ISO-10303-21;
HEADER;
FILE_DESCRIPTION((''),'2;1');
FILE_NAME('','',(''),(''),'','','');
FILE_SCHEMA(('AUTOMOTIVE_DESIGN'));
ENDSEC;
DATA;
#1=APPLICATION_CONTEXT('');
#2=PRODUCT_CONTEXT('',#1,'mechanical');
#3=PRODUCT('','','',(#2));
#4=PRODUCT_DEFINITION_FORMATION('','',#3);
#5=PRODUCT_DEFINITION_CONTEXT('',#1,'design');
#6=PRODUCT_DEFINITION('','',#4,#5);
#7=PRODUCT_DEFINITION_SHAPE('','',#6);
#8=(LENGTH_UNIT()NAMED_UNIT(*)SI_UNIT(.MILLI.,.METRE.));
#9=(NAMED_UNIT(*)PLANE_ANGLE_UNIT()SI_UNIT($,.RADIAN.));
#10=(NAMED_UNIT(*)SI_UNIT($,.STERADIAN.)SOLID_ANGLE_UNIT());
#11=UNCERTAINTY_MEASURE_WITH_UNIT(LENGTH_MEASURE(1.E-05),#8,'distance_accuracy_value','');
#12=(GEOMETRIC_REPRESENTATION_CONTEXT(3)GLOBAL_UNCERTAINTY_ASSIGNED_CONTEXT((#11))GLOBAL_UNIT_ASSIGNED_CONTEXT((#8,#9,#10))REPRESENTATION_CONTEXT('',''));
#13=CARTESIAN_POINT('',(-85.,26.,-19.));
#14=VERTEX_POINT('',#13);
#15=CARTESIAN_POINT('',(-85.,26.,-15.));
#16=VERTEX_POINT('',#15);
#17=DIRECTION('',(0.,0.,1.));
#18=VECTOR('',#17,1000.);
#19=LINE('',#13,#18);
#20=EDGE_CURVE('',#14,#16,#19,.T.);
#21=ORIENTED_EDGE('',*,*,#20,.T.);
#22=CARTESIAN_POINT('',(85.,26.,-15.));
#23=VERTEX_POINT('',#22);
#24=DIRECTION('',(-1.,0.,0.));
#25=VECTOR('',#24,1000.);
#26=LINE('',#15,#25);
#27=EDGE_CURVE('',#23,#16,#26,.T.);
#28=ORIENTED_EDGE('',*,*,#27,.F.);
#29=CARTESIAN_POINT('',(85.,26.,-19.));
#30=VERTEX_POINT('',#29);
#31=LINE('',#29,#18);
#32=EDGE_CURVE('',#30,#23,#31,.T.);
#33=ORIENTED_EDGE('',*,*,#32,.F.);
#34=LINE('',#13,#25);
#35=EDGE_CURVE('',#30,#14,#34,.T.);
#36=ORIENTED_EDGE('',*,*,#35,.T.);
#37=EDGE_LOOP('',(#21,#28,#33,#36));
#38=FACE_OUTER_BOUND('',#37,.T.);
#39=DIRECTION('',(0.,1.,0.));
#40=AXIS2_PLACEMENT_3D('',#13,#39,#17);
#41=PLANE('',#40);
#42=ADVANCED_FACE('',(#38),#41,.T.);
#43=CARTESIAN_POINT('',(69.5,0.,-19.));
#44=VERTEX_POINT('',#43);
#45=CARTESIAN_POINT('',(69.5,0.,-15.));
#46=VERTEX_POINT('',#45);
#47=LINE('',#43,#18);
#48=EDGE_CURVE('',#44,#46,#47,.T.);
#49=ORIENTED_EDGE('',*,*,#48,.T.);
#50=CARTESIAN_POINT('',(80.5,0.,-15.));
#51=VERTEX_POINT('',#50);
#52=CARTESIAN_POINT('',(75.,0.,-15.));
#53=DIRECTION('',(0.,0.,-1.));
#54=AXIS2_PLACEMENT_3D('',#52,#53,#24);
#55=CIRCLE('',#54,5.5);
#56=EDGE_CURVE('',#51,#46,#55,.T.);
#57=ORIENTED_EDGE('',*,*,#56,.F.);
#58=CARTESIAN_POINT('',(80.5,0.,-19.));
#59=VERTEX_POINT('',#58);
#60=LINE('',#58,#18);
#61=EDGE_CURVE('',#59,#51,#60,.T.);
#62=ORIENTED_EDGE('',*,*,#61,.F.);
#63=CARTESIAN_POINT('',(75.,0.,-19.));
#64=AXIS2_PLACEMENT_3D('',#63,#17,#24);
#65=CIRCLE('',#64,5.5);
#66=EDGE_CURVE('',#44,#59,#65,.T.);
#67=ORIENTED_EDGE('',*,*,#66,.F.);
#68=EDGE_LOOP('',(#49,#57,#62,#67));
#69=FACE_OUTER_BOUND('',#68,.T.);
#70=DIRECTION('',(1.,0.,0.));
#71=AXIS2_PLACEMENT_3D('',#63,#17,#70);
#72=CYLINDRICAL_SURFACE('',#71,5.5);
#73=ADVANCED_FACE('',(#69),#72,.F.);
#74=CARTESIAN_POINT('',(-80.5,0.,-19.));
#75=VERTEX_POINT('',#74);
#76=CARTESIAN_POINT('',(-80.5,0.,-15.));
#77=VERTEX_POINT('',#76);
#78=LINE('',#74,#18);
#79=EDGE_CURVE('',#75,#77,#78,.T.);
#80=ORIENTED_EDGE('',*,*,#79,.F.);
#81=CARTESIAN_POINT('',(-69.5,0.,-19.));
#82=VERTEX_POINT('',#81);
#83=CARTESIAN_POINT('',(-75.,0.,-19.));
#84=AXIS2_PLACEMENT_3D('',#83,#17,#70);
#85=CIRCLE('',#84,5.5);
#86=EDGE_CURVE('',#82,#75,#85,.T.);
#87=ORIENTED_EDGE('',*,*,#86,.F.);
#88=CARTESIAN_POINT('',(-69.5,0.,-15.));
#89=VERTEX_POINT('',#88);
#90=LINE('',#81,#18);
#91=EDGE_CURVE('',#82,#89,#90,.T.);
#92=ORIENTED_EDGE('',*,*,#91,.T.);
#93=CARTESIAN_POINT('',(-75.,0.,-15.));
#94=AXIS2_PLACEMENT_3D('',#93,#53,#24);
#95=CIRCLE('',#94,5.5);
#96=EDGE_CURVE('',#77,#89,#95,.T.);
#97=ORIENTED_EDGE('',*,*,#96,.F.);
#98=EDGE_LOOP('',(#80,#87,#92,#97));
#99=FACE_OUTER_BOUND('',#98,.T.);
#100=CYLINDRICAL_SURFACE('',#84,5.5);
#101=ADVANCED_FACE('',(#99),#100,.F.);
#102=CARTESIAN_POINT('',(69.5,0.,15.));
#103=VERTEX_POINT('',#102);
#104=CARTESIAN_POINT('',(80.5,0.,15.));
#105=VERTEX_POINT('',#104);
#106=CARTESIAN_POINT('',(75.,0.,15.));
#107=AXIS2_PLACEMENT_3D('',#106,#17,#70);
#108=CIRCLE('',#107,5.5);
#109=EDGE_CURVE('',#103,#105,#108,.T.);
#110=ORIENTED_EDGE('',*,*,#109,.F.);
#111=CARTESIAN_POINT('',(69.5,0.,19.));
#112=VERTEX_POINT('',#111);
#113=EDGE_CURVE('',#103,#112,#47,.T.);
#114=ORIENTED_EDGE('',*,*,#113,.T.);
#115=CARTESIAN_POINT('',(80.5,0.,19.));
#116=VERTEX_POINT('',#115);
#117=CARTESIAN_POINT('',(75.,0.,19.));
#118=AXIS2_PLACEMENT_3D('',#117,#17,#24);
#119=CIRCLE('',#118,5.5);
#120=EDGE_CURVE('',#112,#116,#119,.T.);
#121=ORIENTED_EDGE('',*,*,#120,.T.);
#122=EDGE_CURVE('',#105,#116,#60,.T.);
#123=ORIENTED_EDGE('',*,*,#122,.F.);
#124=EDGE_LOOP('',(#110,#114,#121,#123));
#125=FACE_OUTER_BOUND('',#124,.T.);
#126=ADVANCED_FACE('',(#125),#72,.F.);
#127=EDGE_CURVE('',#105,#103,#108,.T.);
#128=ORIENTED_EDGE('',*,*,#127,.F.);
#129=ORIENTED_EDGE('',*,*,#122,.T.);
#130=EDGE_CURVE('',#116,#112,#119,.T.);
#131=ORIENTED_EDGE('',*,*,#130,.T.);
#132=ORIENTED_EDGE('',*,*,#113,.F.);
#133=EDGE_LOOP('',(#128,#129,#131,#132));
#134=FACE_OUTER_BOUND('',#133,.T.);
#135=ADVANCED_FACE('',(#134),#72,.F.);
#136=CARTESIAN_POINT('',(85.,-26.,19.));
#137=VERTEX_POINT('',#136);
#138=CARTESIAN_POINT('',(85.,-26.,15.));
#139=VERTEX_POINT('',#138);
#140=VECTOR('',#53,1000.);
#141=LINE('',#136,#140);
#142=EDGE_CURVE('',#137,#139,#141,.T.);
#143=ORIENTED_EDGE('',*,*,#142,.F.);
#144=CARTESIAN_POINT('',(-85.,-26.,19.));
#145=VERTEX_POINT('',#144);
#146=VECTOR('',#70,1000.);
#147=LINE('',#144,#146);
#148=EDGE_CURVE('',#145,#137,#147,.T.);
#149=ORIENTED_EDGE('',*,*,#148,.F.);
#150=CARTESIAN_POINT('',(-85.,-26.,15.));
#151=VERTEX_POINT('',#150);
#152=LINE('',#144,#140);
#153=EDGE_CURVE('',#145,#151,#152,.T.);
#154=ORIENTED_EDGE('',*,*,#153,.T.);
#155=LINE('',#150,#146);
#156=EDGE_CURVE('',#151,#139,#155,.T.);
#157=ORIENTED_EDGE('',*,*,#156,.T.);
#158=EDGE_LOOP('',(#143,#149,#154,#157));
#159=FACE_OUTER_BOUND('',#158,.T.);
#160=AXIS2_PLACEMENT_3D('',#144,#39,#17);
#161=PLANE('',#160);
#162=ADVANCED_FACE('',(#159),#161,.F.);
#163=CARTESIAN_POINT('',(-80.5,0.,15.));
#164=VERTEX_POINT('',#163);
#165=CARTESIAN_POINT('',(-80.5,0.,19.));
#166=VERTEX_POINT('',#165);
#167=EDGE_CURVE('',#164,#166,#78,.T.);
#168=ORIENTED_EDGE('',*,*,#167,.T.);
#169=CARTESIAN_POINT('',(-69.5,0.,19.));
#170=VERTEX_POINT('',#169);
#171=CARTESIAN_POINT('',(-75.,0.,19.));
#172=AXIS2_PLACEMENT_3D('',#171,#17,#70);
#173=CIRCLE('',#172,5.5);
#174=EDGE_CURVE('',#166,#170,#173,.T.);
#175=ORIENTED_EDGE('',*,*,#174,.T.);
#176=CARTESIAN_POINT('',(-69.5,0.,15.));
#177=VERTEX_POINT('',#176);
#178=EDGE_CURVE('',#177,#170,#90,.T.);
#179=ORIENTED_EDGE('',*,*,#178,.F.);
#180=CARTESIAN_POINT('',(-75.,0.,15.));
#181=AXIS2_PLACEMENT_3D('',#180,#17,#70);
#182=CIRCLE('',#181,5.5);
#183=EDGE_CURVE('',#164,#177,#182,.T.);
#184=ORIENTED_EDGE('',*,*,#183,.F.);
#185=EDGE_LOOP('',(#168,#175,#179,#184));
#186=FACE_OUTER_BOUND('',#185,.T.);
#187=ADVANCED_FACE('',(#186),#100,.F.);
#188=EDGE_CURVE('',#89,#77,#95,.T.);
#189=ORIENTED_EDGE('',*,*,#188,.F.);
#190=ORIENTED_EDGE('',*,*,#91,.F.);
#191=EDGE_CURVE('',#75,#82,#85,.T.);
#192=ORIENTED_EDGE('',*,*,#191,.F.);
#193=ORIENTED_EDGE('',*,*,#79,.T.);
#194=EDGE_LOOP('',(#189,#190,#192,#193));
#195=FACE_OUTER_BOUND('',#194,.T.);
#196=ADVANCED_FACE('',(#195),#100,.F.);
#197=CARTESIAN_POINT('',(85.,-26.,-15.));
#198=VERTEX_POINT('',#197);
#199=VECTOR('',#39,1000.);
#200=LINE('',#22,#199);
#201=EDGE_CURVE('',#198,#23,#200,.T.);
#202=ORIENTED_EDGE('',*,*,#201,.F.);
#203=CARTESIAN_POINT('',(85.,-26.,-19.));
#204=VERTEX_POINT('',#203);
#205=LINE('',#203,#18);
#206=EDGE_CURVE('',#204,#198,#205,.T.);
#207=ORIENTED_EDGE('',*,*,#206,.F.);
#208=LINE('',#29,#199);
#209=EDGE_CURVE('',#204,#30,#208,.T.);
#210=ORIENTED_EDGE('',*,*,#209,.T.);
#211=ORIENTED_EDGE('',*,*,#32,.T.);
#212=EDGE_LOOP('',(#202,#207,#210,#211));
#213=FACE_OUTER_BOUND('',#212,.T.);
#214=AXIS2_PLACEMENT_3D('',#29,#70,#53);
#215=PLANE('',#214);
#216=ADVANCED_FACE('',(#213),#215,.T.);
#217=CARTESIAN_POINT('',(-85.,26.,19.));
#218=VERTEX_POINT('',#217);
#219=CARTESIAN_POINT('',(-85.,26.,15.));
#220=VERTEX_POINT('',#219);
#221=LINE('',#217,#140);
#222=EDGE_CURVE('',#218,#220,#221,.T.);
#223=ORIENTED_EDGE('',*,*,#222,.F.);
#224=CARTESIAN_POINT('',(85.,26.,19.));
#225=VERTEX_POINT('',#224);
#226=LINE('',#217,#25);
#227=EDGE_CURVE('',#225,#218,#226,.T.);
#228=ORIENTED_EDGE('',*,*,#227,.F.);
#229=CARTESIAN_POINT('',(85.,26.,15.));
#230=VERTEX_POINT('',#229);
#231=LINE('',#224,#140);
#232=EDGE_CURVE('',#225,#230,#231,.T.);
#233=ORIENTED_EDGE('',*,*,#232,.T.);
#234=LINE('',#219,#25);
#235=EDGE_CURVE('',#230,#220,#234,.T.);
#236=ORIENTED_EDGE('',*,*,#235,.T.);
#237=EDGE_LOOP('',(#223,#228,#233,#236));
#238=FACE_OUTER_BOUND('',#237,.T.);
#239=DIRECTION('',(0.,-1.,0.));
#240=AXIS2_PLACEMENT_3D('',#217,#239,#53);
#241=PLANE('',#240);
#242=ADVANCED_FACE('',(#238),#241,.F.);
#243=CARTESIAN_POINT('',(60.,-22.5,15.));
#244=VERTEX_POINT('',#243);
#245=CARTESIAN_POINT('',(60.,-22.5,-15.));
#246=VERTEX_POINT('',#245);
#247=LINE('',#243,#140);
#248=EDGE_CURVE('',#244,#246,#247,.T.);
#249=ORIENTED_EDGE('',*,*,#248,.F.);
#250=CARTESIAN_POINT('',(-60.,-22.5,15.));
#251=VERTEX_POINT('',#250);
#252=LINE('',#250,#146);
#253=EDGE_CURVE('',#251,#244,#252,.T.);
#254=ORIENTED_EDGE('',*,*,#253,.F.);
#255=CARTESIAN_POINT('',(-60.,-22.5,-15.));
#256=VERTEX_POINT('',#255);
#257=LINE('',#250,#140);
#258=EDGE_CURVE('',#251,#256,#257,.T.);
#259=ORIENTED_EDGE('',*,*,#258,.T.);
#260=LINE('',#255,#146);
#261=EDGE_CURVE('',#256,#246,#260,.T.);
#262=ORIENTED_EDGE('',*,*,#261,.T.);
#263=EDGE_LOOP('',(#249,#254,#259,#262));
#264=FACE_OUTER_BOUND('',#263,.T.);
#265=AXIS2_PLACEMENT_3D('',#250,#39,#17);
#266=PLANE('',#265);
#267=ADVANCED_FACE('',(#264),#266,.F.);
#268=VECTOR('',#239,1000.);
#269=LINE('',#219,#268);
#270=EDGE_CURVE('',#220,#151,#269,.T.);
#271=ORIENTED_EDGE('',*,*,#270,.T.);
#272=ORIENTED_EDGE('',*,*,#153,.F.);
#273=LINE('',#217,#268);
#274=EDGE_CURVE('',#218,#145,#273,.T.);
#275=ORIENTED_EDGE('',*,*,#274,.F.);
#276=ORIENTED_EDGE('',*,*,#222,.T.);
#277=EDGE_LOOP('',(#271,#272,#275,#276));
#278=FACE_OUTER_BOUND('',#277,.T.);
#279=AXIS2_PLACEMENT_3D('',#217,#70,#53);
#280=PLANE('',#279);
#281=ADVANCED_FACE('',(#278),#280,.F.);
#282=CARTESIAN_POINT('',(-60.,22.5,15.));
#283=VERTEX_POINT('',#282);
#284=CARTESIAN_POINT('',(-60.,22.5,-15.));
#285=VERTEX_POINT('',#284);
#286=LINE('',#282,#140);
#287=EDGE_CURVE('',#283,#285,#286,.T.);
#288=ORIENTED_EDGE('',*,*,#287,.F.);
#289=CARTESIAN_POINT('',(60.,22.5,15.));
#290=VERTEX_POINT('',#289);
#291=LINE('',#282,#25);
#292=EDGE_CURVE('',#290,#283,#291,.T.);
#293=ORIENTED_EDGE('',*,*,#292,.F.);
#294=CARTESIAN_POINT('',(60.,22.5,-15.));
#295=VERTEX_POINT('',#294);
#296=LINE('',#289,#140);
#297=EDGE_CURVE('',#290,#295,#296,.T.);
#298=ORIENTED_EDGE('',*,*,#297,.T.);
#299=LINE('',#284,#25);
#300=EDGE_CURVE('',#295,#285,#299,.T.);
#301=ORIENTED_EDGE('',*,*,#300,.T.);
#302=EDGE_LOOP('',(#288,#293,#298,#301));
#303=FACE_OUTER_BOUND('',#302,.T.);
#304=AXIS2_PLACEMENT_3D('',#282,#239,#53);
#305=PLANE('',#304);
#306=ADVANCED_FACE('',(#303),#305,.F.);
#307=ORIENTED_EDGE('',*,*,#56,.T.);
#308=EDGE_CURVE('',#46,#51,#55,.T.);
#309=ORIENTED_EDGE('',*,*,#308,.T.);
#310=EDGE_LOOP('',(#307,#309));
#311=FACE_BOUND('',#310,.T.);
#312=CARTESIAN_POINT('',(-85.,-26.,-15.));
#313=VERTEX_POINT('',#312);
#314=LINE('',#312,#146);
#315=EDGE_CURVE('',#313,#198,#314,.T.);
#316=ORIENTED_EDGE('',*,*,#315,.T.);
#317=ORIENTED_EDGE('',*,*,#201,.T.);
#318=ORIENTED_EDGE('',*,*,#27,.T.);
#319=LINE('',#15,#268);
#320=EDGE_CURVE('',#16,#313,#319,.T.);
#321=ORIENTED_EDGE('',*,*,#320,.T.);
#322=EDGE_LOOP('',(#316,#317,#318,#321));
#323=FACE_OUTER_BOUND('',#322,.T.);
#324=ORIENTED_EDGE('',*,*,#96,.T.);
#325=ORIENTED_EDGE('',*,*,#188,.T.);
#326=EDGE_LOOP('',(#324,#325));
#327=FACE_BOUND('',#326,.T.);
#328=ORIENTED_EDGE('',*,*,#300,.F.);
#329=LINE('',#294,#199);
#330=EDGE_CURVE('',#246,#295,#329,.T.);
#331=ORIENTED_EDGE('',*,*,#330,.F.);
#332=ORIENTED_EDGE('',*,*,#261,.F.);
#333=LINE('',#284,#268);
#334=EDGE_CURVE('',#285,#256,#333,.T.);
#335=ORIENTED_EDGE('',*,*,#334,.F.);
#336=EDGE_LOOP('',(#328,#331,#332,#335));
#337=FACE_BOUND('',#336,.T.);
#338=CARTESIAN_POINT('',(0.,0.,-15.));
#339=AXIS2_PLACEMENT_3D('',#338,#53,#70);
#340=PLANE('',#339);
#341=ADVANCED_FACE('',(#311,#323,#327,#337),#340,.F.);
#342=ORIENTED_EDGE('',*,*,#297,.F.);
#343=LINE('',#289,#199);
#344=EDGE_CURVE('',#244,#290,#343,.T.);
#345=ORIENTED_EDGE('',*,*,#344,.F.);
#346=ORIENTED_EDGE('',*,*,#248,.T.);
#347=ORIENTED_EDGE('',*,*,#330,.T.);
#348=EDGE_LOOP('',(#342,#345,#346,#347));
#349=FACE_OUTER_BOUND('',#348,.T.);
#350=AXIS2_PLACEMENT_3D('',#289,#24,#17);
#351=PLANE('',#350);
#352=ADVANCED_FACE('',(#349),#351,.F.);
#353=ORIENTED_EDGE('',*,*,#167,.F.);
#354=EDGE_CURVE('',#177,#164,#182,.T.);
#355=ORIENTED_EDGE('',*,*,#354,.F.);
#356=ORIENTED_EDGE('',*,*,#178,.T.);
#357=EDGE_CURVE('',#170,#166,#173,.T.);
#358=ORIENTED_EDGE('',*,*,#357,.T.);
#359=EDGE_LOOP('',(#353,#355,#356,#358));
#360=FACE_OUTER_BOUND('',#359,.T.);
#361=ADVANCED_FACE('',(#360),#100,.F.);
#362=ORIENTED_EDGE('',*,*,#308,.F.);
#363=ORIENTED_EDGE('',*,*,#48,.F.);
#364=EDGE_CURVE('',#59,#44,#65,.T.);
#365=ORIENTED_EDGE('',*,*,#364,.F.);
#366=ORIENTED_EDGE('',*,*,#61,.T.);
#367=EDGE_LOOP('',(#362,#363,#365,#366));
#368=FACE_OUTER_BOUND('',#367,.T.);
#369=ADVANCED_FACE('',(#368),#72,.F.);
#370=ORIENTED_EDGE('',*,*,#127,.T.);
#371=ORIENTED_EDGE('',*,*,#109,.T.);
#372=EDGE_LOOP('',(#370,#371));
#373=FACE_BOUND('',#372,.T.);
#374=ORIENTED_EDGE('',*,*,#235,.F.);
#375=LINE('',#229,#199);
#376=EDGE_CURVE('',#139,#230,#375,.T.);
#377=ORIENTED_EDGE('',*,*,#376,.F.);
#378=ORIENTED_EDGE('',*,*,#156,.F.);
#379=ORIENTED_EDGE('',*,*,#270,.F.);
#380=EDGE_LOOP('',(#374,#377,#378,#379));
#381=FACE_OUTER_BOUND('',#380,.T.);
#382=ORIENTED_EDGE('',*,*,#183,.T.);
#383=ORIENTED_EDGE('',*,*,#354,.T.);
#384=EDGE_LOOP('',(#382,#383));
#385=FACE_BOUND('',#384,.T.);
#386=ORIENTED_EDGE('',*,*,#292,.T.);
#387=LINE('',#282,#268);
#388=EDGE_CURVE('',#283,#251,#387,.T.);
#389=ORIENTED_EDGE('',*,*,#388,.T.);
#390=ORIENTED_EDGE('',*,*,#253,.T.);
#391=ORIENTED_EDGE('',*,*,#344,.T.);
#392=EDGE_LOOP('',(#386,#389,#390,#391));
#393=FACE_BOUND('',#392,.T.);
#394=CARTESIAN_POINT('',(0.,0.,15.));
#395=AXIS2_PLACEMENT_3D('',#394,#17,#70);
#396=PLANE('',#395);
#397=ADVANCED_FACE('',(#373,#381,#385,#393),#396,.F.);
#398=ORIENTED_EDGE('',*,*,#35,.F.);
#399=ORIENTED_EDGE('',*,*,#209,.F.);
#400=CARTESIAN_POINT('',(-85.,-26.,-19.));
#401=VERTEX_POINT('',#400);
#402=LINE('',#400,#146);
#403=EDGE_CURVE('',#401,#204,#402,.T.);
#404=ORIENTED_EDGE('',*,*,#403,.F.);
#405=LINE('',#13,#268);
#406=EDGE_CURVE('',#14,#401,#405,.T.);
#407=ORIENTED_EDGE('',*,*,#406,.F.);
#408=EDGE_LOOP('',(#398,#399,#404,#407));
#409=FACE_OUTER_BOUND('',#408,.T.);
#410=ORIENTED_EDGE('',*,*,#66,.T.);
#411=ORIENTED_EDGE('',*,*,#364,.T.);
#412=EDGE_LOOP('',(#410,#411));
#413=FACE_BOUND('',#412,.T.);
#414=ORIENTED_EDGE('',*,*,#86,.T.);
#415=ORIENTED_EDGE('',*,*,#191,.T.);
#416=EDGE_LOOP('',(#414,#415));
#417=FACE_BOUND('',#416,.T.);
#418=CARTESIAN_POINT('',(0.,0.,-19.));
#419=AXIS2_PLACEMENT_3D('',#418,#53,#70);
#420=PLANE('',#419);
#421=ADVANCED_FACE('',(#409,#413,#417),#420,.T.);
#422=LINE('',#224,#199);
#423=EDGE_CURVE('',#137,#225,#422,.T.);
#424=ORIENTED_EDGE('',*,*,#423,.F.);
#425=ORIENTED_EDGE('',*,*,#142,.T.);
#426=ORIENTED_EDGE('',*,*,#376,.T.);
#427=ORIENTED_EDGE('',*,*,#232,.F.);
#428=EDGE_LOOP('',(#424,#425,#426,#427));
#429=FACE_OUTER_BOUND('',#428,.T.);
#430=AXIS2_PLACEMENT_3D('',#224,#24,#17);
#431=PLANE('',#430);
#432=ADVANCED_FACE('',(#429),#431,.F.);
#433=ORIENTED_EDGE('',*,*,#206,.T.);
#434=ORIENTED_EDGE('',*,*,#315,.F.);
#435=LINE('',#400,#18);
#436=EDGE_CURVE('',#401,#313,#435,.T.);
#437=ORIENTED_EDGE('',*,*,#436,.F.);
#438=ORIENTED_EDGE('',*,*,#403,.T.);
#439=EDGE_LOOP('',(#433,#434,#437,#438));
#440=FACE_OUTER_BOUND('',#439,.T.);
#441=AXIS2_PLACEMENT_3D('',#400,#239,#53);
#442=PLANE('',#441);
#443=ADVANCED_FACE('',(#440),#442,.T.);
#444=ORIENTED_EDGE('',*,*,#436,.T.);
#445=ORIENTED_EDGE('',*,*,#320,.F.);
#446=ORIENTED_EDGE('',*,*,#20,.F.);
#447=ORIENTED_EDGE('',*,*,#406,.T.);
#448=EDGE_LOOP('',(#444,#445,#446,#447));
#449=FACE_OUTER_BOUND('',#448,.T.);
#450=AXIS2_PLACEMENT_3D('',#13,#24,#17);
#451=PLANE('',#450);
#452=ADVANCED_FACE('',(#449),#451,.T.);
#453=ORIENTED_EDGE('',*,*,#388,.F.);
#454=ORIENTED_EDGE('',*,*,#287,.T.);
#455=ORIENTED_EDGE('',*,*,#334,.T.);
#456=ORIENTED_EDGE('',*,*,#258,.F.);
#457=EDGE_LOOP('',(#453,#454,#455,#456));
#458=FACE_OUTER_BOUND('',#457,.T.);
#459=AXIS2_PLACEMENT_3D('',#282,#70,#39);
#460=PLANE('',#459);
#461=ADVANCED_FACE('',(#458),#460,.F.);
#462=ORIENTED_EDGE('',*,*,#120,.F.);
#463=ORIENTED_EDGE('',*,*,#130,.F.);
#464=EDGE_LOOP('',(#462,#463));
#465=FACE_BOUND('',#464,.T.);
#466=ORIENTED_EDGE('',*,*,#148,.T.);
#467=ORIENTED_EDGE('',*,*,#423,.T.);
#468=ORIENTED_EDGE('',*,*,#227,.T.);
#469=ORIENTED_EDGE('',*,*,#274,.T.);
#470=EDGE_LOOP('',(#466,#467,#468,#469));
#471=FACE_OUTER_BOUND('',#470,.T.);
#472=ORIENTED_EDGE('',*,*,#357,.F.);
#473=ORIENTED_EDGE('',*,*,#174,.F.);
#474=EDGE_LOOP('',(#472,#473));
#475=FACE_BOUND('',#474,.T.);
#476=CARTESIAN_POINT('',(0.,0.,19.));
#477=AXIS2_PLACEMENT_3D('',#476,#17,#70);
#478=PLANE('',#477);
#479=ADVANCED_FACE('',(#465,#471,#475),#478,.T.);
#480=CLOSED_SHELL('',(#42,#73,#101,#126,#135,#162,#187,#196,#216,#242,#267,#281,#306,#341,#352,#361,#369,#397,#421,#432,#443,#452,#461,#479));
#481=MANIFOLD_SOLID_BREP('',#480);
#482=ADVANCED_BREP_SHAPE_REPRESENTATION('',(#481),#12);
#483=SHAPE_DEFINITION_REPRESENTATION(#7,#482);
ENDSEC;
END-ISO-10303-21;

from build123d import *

# Parameters (mm, degrees)
SKETCH_1_W          = 120
SKETCH_1_H          = 45
EXTRUDE_1_DEPTH     = 15
SKETCH_2_W          = 170
SKETCH_2_H          = 52
EXTRUDE_2_DEPTH     = 4
SKETCH_3_R          = 5.5
CUT_EXTRUDE_1_DEPTH = 97.669540187


with BuildPart() as part:
    # 草图1 → 凸台-拉伸1 (new, symmetric)
    with BuildSketch(Plane.XY):
        Rectangle(SKETCH_1_W, SKETCH_1_H)
    extrude(amount=EXTRUDE_1_DEPTH, both=True)

    # 草图2 → 凸台-拉伸2 (add)
    with BuildSketch(Plane.XY.offset(15)):
        Rectangle(SKETCH_2_W, SKETCH_2_H)
    extrude_2 = extrude(amount=EXTRUDE_2_DEPTH)

    # 镜向1: 凸台-拉伸2 across plane
    add(extrude_2.mirror(Plane.XY))

    # 草图3 → 切除-拉伸1 (cut, through all)
    with BuildSketch(Plane.XY.offset(19)):
        with Locations((-75, 0)):
            Circle(SKETCH_3_R)
        with Locations(Location((75, 0, 0), (0, 0, 180))):
            Circle(SKETCH_3_R)
    extrude(amount=-CUT_EXTRUDE_1_DEPTH, mode=Mode.SUBTRACT)


solid = part.part
